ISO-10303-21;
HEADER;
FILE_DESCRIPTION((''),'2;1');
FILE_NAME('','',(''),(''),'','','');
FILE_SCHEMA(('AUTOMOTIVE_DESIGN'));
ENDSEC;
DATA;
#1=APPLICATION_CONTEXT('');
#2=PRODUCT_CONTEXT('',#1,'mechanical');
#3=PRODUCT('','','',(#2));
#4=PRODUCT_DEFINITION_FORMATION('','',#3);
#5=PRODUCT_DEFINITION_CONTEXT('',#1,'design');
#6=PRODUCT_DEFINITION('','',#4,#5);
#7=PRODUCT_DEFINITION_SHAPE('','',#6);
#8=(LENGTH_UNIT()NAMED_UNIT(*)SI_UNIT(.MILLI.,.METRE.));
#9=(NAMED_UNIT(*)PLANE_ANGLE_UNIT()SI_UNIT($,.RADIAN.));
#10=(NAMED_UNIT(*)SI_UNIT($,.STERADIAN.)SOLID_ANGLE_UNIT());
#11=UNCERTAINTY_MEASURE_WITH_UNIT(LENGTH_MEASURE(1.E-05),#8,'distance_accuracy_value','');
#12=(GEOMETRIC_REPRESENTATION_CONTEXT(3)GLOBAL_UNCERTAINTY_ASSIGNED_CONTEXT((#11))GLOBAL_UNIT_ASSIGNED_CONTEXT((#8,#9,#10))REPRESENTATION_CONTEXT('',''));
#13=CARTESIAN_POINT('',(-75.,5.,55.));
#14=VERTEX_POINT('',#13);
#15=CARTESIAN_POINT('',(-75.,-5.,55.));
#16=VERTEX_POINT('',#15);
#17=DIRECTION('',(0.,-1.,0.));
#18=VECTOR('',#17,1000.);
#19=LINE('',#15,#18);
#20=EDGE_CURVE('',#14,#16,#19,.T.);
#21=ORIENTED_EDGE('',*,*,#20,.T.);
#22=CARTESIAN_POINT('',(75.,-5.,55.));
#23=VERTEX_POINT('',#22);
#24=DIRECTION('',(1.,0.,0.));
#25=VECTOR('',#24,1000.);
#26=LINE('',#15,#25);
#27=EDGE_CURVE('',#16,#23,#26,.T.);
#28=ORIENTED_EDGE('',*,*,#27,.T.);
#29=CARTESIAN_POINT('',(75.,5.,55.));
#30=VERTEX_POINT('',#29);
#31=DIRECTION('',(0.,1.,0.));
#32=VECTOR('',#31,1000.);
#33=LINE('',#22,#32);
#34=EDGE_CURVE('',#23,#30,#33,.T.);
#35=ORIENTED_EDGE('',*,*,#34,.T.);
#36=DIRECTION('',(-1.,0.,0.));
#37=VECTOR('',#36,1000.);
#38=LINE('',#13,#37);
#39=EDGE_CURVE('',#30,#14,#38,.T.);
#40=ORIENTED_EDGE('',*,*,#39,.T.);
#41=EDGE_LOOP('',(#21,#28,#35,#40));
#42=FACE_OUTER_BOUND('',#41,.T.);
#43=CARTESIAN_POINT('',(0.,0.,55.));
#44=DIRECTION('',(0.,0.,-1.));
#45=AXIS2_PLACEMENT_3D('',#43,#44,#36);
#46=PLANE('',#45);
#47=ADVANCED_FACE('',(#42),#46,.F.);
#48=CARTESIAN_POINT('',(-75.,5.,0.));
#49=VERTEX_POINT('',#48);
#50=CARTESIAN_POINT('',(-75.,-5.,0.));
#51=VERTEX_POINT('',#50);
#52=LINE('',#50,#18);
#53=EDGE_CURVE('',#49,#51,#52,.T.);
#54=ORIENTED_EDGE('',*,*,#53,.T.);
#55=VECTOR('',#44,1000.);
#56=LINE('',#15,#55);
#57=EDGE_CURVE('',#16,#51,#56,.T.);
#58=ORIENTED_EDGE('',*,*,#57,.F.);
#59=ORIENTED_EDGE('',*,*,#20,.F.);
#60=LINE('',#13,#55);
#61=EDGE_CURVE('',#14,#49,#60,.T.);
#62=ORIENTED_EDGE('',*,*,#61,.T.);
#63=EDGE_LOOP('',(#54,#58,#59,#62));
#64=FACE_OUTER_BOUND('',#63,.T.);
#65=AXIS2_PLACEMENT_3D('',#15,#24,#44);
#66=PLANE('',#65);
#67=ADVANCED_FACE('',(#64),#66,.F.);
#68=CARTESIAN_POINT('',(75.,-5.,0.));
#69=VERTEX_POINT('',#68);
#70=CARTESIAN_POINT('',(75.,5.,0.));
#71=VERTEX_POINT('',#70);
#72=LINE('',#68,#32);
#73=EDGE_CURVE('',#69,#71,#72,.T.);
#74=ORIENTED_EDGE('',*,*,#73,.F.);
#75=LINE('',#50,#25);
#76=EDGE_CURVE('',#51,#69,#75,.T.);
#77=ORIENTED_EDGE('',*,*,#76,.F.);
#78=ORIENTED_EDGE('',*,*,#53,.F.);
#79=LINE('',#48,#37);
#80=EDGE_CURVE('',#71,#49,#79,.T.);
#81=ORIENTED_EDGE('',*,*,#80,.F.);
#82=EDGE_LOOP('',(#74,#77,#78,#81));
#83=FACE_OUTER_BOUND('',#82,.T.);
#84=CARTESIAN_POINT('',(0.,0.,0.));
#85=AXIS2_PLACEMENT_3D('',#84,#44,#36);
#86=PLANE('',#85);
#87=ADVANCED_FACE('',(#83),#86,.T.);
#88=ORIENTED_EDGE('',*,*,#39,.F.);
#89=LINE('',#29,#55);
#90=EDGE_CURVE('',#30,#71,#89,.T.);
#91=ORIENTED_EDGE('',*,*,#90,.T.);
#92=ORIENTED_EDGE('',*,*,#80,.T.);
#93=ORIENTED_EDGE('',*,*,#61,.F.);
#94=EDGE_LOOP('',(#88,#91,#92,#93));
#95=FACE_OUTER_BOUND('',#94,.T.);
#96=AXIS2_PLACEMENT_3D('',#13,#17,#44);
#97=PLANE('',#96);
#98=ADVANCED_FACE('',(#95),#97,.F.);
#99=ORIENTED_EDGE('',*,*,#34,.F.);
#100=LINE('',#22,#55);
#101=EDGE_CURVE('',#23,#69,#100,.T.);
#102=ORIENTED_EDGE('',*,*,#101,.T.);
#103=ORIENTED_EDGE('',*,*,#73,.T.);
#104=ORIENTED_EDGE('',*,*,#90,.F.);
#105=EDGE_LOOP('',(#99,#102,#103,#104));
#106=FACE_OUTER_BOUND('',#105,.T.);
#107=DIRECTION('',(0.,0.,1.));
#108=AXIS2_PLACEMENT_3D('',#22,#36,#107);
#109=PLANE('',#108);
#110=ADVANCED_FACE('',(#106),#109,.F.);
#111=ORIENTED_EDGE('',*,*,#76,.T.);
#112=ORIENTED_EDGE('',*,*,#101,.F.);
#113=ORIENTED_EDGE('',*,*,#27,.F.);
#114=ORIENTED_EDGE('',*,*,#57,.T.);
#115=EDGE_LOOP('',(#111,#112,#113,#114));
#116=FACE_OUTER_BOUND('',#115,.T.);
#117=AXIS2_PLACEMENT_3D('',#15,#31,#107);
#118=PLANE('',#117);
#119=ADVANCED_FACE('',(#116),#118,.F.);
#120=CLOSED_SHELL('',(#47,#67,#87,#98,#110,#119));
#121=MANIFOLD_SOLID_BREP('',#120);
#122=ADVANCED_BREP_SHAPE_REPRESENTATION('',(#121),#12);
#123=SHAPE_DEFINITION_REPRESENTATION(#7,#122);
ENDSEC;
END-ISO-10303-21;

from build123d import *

# Parameters (mm, degrees)
SKETCH_1_W      = 150
SKETCH_1_H      = 10
EXTRUDE_1_DEPTH = 55


with BuildPart() as part:
    # 草图1 → 凸台-拉伸1 (new body)
    with BuildSketch(Plane.XY):
        Rectangle(SKETCH_1_W, SKETCH_1_H)
    extrude(amount=EXTRUDE_1_DEPTH)


solid = part.part
